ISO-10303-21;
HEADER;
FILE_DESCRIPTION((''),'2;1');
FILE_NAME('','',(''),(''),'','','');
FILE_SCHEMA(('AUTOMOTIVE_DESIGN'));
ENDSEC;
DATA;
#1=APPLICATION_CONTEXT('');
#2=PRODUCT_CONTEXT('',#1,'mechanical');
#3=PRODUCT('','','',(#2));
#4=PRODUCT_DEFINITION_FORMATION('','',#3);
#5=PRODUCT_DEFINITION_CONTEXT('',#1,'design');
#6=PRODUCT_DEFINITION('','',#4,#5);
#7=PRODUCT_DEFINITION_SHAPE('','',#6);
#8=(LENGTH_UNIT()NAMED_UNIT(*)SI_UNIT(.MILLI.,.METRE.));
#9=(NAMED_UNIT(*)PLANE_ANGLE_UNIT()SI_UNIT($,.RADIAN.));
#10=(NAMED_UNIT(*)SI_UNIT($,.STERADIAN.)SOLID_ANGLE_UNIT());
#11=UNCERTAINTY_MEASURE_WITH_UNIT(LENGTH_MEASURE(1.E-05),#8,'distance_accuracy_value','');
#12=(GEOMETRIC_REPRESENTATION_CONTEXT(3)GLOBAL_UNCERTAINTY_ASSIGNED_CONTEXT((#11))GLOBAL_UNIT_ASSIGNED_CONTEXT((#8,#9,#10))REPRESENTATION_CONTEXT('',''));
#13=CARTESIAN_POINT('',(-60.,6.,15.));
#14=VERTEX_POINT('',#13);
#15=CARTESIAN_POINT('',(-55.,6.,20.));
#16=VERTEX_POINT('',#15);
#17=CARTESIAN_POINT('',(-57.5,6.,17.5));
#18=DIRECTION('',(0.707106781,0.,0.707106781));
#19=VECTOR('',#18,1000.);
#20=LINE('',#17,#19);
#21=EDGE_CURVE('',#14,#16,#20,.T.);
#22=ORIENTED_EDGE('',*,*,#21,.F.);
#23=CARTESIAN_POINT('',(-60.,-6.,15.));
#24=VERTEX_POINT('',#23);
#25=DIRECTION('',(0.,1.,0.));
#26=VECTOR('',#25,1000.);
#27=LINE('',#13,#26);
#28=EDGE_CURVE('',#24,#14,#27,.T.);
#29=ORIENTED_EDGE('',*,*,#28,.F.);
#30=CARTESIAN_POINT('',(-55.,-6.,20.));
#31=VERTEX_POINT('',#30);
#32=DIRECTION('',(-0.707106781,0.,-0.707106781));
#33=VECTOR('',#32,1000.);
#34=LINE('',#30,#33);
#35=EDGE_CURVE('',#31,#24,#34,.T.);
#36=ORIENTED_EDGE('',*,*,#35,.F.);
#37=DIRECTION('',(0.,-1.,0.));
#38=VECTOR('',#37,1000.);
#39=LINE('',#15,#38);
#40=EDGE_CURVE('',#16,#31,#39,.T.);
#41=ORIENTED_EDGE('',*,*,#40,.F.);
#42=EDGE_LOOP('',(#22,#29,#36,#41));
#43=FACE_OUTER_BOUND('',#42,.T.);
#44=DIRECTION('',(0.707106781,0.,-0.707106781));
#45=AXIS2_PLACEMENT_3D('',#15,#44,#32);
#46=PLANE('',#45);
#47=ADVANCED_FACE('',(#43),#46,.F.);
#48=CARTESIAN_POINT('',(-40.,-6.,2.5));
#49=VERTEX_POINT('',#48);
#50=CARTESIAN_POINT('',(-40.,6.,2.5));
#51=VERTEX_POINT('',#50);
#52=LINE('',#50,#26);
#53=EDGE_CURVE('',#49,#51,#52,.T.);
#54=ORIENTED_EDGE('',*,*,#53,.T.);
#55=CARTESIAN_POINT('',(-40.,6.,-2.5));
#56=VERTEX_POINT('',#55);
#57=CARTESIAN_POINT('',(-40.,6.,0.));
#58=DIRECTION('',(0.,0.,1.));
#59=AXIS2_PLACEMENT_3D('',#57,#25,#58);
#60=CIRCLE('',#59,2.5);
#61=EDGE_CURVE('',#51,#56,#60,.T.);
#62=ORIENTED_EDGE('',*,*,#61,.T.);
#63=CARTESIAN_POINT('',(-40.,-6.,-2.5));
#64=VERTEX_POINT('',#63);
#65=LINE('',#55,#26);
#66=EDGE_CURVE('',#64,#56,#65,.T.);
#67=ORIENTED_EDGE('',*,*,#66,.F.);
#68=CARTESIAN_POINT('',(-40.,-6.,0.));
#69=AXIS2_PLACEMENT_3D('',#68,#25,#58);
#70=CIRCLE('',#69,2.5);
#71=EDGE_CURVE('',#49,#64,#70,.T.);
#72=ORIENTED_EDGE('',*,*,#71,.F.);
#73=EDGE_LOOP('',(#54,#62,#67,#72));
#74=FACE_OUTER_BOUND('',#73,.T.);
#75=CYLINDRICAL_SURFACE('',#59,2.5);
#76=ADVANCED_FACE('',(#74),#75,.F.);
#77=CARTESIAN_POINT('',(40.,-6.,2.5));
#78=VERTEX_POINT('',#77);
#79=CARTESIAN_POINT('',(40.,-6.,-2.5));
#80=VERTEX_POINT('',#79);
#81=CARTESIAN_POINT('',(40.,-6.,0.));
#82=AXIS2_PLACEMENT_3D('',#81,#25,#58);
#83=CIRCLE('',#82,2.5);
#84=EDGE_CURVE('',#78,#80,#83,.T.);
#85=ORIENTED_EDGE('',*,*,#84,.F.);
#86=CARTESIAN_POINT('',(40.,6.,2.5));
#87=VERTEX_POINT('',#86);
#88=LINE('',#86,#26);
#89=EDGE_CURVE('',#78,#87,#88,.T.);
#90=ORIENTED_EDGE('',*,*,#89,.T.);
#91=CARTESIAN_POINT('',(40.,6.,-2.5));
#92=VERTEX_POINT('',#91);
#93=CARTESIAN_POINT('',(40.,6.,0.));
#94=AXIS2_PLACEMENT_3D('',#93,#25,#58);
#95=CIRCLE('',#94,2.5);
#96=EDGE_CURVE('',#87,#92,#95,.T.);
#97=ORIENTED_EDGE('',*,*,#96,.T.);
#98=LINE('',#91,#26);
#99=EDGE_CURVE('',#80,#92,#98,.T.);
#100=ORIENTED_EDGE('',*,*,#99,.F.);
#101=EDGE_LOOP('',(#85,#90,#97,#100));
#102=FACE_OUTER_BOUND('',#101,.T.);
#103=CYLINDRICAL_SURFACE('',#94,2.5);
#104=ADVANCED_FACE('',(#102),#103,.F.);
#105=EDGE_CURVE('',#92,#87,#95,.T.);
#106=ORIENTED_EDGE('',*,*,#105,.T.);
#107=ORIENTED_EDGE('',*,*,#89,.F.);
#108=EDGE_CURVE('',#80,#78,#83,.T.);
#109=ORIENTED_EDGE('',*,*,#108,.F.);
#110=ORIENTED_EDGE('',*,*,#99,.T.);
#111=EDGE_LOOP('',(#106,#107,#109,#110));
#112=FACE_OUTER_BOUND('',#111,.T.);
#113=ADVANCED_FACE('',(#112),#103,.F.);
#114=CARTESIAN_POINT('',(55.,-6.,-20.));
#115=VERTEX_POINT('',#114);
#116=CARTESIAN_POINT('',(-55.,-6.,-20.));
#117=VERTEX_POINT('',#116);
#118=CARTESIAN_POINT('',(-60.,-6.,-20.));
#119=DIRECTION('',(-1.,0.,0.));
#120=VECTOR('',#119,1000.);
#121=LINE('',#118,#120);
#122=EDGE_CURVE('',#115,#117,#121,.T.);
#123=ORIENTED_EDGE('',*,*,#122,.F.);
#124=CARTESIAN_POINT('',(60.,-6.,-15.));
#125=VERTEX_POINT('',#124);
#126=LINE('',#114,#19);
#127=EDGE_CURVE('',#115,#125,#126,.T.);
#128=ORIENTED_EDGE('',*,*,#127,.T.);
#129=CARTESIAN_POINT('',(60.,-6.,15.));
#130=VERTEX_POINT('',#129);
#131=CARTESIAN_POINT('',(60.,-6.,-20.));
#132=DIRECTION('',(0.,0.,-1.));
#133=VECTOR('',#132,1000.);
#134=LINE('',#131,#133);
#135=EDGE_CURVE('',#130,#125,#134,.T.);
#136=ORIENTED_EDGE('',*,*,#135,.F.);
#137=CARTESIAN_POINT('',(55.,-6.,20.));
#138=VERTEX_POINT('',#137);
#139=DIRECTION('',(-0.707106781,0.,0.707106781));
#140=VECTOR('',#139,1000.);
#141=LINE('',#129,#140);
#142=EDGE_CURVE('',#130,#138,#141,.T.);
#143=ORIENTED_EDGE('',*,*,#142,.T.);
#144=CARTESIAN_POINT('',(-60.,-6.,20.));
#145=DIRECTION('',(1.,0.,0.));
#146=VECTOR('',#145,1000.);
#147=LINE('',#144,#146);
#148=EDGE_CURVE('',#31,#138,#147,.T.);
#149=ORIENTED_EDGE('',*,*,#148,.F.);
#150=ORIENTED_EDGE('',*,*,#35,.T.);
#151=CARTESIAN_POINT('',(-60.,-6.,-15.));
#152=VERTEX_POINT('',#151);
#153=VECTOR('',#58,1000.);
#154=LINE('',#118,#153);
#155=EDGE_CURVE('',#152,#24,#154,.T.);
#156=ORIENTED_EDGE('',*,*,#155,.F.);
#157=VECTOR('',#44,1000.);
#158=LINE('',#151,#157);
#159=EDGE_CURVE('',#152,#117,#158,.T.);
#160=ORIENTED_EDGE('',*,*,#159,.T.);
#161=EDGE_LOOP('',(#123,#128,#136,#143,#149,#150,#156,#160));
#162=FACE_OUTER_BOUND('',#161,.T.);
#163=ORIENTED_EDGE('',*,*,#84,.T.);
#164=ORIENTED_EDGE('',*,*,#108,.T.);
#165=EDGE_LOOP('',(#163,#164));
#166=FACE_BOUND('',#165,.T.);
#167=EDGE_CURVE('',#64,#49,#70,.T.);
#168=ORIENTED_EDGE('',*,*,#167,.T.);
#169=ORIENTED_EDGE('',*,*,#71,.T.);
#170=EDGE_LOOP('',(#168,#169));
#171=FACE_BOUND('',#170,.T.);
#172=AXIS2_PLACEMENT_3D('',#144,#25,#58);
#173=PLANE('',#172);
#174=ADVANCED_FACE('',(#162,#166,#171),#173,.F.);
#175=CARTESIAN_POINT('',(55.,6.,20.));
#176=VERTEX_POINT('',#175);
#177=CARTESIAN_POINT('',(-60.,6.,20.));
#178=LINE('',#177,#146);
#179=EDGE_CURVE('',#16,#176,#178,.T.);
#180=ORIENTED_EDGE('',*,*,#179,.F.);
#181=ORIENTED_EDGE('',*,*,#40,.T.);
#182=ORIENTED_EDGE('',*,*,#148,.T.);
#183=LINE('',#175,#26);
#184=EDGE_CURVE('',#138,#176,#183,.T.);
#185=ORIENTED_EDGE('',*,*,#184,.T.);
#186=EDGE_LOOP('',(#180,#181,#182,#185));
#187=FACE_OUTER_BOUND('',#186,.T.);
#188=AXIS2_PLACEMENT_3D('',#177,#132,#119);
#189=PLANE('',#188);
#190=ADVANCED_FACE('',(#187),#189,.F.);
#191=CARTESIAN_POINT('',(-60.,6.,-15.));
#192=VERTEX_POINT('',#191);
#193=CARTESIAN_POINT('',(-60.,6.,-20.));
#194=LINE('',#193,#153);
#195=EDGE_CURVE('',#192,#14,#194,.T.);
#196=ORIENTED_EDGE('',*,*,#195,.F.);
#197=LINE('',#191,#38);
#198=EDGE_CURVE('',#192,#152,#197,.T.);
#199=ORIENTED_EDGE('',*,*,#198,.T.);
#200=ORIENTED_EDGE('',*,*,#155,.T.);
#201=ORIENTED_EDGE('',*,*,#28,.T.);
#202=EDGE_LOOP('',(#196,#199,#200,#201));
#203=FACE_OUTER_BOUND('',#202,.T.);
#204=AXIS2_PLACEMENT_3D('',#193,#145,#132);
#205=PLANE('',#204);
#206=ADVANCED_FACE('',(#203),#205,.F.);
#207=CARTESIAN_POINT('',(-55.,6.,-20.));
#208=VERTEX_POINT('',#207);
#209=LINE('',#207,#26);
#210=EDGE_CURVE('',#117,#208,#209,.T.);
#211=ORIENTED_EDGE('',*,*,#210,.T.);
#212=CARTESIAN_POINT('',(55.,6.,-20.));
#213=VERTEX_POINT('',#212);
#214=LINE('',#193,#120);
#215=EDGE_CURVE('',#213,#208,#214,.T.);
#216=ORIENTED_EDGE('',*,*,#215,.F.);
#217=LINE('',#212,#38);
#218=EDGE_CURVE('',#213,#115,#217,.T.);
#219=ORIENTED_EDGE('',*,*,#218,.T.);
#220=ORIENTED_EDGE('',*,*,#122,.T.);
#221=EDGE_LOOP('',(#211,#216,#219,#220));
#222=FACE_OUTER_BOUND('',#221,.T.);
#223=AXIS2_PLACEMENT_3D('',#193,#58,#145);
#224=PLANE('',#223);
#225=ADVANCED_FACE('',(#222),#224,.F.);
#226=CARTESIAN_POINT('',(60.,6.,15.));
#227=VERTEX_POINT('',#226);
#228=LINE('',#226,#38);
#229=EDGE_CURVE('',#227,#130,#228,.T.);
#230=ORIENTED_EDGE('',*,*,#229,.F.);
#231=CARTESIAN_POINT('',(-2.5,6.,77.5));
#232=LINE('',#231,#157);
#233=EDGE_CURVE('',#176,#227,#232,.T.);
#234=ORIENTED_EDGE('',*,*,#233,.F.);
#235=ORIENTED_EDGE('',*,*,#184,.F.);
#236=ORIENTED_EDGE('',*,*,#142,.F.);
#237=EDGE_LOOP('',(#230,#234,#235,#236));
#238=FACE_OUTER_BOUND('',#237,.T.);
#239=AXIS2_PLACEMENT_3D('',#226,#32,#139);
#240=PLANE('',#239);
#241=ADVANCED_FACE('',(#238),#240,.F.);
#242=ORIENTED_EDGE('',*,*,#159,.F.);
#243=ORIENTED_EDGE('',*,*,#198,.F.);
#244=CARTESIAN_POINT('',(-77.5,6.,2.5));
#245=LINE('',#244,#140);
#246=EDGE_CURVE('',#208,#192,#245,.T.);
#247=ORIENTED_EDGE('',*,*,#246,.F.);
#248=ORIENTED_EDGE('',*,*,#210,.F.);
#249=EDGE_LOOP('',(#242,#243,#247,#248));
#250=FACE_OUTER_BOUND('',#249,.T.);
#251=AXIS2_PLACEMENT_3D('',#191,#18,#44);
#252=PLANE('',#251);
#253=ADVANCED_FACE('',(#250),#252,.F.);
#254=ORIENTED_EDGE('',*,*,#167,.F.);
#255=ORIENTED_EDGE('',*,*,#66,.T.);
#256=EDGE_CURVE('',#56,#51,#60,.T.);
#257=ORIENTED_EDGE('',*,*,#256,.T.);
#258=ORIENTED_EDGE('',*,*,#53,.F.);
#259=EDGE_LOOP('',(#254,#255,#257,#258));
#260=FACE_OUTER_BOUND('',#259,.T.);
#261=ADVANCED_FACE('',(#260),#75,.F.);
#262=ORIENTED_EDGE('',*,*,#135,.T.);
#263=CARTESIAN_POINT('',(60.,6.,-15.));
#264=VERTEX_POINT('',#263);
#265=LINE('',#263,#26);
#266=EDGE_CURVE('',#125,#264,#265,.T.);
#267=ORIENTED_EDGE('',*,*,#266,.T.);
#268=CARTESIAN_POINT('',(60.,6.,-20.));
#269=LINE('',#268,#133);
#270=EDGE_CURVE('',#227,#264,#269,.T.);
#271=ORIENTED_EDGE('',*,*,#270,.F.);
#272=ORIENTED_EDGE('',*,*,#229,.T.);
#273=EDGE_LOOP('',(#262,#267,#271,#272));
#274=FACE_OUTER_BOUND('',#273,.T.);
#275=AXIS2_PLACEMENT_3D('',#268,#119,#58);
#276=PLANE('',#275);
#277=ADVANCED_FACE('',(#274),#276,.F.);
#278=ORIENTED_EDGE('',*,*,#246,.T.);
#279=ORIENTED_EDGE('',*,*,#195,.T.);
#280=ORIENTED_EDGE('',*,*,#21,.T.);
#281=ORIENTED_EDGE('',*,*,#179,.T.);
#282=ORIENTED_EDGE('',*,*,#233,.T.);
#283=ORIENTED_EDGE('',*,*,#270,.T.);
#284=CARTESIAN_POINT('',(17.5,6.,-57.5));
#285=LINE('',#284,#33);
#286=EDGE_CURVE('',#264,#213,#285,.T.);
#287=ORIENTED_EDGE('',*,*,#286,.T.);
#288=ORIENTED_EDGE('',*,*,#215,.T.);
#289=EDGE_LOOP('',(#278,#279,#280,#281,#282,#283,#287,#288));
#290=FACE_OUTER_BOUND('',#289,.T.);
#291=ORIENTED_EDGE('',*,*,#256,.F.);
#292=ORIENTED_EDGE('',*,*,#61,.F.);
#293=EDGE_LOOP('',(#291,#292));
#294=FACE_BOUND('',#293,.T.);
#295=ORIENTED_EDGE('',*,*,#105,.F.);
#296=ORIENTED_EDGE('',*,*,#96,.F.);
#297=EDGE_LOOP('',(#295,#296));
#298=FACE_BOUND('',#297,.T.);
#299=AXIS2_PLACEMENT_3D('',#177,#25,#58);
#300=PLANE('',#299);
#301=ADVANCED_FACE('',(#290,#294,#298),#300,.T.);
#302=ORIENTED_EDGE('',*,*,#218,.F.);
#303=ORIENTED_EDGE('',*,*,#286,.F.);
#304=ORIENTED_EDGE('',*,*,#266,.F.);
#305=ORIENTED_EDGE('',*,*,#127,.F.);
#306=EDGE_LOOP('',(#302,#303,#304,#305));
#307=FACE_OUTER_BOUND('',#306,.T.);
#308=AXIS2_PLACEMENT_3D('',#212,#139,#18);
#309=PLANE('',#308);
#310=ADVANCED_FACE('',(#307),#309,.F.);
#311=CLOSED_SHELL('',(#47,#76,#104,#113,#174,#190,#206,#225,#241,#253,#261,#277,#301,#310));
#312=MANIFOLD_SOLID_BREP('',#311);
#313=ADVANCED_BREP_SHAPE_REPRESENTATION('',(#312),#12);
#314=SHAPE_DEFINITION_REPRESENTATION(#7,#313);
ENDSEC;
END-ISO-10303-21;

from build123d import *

# Parameters (mm, degrees)
SKETCH1_W             = 120
SKETCH1_H             = 40
EXTRUDE1_DEPTH        = 6
M6_TAPPED_HOLE1_D     = 5
M6_TAPPED_HOLE1_DEPTH = 15
M6_TAPPED_HOLE1_TIP   = 1.502151548
CHAMFER1_SIZE         = 5


with BuildPart() as part:
    # Sketch1 → Extrude1 (new, symmetric)
    with BuildSketch(Plane(origin=(0, 0, 0), x_dir=(1, 0, 0), z_dir=(0, 1, 0))):
        Rectangle(SKETCH1_W, SKETCH1_H)
    extrude(amount=EXTRUDE1_DEPTH, both=True)

    # M6 Tapped Hole1
    with Locations(Plane(origin=(0, 6, 0), x_dir=(-1, 0, 0), z_dir=(0, 1, 0))):
        with Locations((40, 0), (-40, 0)):
            Hole(M6_TAPPED_HOLE1_D / 2, depth=M6_TAPPED_HOLE1_DEPTH)
            with Locations((0, 0, -(M6_TAPPED_HOLE1_DEPTH + M6_TAPPED_HOLE1_TIP / 2))):  # 118° drill point
                Cone(0, M6_TAPPED_HOLE1_D / 2, M6_TAPPED_HOLE1_TIP, mode=Mode.SUBTRACT)

    # Chamfer1
    chamfer1_edges = [part.edges().sort_by_distance(p)[0] for p in [
        (-60, 0, -20),
        (60, 0, -20),
        (60, 0, 20),
        (-60, 0, 20),
    ]]
    chamfer(chamfer1_edges, length=CHAMFER1_SIZE)


solid = part.part
